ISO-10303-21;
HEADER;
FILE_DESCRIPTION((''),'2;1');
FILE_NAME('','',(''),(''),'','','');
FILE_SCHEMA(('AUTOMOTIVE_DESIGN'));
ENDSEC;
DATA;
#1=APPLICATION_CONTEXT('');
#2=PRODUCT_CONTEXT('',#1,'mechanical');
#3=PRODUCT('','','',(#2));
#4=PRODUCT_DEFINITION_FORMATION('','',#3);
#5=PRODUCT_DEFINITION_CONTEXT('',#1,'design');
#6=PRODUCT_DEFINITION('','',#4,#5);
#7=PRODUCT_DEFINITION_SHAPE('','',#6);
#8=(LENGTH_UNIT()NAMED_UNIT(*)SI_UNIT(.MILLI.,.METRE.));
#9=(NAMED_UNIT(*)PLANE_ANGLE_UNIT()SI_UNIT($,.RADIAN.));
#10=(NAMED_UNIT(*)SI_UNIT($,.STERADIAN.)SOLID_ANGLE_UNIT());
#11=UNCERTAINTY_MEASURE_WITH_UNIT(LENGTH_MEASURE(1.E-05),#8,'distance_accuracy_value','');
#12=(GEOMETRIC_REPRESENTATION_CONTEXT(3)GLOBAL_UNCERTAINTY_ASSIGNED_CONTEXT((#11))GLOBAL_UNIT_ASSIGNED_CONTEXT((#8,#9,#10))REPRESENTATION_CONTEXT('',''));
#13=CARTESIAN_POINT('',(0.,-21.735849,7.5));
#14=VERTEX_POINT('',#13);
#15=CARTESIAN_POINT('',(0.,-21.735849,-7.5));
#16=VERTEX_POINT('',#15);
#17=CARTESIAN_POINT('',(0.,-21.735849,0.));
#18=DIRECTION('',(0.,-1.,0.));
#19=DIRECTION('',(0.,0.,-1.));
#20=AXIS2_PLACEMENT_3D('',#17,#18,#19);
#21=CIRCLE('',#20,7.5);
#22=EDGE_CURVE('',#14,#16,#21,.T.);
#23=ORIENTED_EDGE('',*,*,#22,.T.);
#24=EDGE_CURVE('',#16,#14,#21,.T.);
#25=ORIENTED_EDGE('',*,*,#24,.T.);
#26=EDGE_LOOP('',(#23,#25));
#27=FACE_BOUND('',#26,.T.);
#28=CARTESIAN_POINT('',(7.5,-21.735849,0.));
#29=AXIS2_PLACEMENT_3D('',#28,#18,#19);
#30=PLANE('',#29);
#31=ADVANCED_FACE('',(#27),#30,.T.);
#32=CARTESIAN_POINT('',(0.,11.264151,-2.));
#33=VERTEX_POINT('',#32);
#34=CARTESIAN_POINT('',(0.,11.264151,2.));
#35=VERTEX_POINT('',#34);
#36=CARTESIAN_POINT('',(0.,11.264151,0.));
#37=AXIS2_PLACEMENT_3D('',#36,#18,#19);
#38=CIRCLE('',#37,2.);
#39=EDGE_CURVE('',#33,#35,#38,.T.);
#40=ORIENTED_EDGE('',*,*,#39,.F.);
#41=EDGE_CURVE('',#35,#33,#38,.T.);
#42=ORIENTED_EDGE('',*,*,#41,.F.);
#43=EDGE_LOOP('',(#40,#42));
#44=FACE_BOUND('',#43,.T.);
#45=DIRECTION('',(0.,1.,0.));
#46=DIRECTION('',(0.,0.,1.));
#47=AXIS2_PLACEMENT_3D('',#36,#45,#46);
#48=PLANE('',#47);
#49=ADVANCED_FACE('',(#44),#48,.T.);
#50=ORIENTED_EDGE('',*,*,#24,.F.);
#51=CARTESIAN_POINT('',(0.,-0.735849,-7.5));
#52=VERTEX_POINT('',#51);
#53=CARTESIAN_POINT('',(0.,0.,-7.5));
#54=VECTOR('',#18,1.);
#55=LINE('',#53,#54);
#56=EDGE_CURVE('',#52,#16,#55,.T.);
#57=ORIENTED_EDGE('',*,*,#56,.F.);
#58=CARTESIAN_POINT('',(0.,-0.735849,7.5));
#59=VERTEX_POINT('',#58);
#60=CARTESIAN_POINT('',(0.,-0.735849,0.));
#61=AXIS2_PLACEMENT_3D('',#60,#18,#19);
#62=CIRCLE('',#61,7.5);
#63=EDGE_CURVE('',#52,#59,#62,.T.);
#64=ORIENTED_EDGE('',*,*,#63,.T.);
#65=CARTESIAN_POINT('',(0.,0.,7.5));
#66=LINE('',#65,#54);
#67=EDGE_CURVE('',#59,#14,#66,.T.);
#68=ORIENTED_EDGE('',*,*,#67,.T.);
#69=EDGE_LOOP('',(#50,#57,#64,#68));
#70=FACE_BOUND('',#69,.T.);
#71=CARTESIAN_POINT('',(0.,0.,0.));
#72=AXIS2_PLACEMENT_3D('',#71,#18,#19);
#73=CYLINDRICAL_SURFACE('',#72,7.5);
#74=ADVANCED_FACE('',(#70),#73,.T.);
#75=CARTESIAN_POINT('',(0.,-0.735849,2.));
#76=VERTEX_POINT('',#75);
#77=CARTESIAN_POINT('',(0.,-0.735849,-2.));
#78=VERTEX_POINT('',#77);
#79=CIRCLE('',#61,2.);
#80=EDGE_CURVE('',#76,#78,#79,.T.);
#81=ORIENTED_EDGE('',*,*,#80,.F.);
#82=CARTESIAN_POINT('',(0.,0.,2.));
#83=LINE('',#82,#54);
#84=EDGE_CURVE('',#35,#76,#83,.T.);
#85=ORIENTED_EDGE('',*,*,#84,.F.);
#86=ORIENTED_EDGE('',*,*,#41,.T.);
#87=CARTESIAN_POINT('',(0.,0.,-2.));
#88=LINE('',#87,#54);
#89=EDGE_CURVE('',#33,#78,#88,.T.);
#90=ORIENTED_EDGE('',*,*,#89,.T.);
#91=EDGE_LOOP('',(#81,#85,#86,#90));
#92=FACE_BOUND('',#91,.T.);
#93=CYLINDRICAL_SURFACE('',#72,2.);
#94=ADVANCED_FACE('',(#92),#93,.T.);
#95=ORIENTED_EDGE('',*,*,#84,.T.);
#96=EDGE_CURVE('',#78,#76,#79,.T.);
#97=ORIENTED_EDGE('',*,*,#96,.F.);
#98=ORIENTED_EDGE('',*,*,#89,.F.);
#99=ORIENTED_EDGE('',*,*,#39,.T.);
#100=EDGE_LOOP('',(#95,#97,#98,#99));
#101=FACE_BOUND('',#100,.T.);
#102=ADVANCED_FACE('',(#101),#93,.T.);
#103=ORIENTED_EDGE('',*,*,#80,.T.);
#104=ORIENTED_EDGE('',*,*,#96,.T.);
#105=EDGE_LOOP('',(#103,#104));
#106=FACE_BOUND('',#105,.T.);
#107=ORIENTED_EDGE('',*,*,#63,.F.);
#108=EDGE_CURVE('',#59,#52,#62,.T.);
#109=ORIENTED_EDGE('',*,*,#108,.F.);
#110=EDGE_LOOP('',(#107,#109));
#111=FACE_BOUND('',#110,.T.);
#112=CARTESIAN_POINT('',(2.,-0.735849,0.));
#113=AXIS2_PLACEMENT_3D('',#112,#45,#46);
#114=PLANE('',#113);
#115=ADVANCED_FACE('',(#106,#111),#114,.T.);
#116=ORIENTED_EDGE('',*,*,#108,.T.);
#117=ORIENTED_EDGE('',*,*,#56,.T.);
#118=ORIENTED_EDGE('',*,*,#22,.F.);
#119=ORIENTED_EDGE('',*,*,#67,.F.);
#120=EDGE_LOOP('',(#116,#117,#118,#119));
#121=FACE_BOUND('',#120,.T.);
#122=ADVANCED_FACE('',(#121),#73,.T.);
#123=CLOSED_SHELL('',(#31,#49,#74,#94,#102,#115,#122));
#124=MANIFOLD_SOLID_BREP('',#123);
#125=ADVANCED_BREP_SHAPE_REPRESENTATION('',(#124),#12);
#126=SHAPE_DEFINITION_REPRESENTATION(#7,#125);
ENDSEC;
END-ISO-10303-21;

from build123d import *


with BuildPart() as part:
    # 草图1 → 旋转1 (revolve)
    with BuildSketch(Plane.XY, mode=Mode.PRIVATE) as revolve_1_sk:
        Polygon((0, 11.264150943), (2, 11.264150943), (2, -0.735849057), (7.5, -0.735849057), (7.5, -21.735849057), (0, -21.735849057), align=None)
    revolve(revolve_1_sk.sketch.rotate(Axis((0, 0, 0), (0, 1, 0)), 90), axis=Axis((0, 0, 0), (0, 1, 0)))


solid = part.part
